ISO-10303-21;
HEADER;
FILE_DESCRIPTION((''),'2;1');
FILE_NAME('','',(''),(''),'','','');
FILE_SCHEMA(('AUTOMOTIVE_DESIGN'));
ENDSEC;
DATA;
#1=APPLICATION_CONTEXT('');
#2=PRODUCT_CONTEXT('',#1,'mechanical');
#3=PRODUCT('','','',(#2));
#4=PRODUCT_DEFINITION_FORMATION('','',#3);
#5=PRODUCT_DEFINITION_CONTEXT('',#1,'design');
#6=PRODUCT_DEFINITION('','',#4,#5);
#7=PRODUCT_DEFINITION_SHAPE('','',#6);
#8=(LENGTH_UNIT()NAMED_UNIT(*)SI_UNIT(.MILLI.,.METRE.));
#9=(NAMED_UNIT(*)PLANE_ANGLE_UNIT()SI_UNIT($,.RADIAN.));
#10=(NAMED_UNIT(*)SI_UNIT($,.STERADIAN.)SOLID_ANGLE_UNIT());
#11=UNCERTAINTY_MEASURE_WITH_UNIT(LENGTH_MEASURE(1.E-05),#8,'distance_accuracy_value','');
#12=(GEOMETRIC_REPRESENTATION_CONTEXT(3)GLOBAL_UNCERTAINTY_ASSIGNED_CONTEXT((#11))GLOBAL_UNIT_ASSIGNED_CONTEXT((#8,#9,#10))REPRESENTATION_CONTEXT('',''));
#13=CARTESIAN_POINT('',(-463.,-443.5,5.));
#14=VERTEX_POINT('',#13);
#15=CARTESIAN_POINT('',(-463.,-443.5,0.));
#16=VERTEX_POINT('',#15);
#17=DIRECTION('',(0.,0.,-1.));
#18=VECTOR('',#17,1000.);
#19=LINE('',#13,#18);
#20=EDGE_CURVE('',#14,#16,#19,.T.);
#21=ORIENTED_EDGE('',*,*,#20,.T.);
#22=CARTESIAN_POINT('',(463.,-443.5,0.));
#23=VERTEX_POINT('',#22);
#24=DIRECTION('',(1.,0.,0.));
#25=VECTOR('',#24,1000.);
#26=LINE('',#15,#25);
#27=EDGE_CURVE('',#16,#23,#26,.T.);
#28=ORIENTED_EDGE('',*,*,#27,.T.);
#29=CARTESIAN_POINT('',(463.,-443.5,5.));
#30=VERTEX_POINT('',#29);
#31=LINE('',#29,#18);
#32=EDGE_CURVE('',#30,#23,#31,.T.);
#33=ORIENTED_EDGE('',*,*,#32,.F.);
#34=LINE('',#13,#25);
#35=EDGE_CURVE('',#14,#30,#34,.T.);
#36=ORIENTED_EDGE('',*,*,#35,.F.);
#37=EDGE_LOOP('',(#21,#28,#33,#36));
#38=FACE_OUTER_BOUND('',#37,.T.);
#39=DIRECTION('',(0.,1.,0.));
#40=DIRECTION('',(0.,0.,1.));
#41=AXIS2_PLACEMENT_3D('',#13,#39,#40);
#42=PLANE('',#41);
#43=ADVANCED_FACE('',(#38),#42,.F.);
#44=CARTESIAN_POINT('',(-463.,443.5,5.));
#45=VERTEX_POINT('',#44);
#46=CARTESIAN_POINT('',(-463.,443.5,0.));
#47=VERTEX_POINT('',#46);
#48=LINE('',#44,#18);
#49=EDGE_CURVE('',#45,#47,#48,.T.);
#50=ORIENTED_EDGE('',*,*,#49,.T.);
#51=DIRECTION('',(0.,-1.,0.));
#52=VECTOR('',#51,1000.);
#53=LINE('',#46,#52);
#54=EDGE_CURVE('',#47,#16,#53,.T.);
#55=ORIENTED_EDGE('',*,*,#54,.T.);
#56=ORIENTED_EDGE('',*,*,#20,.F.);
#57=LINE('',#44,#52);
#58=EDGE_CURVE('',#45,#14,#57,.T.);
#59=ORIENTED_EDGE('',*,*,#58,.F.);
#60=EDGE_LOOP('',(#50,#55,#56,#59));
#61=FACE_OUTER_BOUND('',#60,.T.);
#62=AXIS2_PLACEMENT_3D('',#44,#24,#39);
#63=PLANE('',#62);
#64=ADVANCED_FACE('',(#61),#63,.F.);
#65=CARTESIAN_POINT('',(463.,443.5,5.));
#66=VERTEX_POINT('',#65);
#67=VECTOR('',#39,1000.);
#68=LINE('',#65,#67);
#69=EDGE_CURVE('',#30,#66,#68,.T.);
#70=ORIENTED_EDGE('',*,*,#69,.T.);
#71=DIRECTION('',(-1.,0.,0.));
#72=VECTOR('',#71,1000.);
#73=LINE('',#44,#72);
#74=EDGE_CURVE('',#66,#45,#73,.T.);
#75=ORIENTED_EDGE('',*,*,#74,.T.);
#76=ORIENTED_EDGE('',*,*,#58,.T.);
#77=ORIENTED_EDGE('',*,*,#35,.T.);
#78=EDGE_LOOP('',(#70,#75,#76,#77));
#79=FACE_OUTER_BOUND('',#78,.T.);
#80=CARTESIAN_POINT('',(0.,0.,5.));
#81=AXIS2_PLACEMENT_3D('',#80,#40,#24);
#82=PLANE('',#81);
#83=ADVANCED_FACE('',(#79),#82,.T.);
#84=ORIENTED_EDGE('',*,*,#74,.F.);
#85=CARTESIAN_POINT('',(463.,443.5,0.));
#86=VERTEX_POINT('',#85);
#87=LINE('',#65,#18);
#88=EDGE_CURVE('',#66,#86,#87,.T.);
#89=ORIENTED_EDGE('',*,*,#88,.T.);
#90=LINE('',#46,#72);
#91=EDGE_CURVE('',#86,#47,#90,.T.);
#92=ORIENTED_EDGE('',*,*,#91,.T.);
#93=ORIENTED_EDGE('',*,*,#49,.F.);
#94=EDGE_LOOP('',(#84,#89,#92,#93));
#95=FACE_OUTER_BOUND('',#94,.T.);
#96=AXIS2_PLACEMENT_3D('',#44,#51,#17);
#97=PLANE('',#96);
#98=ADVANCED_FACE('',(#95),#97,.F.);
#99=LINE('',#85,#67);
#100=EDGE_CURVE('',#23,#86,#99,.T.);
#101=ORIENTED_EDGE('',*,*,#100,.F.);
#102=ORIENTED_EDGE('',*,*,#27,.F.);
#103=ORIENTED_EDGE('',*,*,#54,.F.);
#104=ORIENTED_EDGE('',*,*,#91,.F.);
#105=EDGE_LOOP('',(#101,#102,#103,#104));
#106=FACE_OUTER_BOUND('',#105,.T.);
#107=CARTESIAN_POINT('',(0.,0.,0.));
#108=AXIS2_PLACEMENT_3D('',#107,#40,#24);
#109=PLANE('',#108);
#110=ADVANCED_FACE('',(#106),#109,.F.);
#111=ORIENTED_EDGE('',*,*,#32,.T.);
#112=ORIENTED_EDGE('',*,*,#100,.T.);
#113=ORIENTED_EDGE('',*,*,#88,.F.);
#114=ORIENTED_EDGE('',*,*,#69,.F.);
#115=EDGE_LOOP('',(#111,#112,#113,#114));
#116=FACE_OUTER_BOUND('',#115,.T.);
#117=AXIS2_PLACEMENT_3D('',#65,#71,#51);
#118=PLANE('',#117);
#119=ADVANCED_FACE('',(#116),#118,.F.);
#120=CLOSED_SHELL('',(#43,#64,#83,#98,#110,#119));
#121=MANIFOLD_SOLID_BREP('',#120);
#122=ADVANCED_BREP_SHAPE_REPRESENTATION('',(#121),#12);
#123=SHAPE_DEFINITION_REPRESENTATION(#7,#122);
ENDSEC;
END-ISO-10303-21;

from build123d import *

# Parameters (mm, degrees)
SKETCH_1_W      = 926
SKETCH_1_H      = 887
EXTRUDE_1_DEPTH = 5


with BuildPart() as part:
    # 草图1 → 凸台-拉伸1 (new body)
    with BuildSketch(Plane.XY):
        Rectangle(SKETCH_1_W, SKETCH_1_H)
    extrude(amount=EXTRUDE_1_DEPTH)


solid = part.part
